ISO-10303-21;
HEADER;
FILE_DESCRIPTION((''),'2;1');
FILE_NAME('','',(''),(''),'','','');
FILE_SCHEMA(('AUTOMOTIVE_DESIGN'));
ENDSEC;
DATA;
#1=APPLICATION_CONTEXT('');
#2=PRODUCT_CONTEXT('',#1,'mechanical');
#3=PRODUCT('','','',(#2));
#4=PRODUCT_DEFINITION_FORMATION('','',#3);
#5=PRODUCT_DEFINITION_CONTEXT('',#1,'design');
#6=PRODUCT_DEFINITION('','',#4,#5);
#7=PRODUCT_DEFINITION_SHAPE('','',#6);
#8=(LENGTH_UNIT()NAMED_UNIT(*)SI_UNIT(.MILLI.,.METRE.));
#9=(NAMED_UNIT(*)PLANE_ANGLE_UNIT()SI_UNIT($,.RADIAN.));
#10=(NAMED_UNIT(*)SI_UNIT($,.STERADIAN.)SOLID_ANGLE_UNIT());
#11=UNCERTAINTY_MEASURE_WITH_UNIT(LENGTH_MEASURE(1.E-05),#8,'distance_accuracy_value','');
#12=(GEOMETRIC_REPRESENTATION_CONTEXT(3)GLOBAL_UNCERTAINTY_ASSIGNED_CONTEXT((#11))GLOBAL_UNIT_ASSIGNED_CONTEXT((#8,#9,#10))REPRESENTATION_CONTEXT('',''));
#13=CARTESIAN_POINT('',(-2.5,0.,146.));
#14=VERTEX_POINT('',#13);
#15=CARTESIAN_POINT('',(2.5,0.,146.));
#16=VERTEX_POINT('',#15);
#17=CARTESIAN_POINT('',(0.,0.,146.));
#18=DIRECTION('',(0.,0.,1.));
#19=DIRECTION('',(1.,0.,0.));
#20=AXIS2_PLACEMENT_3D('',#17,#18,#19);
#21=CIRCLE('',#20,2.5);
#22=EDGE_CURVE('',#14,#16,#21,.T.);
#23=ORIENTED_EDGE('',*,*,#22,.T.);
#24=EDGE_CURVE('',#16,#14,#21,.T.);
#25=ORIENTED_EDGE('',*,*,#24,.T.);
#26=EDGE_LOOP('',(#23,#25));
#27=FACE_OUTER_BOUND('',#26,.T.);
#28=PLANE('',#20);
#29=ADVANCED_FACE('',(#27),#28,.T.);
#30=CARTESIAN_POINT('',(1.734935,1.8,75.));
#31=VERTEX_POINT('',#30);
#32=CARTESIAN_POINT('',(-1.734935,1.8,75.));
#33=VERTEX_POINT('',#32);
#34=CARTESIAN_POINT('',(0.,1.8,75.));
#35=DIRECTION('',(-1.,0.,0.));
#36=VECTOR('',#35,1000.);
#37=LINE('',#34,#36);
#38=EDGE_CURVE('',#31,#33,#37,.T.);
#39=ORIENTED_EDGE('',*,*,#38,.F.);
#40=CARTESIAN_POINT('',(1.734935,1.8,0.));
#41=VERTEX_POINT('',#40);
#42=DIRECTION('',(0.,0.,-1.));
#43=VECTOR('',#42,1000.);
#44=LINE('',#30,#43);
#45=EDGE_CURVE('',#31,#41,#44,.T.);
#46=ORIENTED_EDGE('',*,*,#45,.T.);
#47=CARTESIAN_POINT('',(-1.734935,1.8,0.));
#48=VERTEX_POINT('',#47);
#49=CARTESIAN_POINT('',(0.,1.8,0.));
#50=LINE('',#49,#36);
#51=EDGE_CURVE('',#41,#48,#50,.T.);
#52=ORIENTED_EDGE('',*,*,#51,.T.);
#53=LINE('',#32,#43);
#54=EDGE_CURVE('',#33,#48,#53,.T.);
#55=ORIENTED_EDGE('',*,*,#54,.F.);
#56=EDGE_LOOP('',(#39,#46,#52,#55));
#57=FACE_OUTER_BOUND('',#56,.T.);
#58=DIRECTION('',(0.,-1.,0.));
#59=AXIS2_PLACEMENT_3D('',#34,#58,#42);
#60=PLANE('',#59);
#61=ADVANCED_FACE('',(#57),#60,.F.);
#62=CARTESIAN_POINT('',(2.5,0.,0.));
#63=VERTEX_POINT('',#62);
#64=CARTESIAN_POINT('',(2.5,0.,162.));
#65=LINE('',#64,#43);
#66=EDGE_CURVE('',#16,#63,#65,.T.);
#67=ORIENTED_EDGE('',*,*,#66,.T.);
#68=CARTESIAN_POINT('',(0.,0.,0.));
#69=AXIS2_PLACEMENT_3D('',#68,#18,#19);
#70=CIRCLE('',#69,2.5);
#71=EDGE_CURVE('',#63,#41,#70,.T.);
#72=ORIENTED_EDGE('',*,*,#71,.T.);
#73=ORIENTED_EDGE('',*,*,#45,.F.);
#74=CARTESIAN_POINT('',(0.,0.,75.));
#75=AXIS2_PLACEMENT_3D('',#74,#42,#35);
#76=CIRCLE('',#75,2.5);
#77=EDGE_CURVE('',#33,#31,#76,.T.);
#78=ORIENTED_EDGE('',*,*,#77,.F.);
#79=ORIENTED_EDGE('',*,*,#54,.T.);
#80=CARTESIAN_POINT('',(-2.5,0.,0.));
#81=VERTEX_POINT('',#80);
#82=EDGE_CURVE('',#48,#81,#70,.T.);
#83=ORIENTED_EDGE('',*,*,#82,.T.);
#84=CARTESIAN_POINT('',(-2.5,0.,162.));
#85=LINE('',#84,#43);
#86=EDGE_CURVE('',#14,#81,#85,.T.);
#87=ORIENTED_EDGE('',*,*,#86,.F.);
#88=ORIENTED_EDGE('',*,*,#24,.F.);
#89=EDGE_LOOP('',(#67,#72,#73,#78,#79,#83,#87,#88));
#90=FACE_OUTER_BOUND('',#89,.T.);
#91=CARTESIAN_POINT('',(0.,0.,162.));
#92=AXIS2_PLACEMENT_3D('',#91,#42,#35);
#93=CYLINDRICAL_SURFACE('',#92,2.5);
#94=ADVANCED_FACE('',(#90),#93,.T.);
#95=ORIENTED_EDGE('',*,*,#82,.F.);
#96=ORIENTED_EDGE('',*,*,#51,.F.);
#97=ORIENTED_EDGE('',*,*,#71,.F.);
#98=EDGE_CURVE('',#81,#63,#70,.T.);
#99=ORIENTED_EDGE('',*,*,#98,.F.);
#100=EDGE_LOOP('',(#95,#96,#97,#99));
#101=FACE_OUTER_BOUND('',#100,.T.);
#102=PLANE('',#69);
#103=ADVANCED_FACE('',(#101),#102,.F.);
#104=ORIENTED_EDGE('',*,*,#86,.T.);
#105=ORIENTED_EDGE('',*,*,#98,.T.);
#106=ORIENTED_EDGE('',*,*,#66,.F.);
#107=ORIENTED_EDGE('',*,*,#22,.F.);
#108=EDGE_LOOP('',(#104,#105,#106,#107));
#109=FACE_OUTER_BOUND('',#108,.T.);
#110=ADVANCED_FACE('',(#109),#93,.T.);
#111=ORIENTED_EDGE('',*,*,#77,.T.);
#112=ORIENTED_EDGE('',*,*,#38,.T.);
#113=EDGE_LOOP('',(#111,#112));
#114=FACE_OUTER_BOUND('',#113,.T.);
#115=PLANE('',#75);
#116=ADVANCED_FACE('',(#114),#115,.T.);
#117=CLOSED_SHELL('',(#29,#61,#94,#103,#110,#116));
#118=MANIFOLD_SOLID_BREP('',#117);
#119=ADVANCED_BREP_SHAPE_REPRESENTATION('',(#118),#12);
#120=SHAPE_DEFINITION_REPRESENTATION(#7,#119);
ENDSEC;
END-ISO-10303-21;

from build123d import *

# Parameters (mm, degrees)
SKETCH1_R           = 2.5
BOSS_EXTRUDE1_DEPTH = 162
CUT_EXTRUDE1_DEPTH  = 75
CUT_EXTRUDE2_START  = -16
SKETCH3_R           = 2.5
CUT_EXTRUDE2_DEPTH  = 16


with BuildPart() as part:
    # Sketch1 → Boss-Extrude1 (new body)
    with BuildSketch(Plane.XY):
        Circle(SKETCH1_R)
    extrude(amount=BOSS_EXTRUDE1_DEPTH)

    # Sketch2 → Cut-Extrude1 (cut)
    with BuildSketch(Plane(origin=(0, 0, 0), x_dir=(-1, 0, 0), z_dir=(0, 0, -1))):
        with BuildLine():
            Line((0, 1.8), (1.734935157, 1.8))
            ThreePointArc((1.734935157, 1.8), (0, 2.5), (-1.734935157, 1.8))
            Line((-1.734935157, 1.8), (0, 1.8))
        make_face()
    extrude(amount=-CUT_EXTRUDE1_DEPTH, mode=Mode.SUBTRACT)

    # Sketch3 → Cut-Extrude2 (cut)
    with BuildSketch(Plane.XY.offset(162).offset(CUT_EXTRUDE2_START)):
        with Locations(Location((0, 0, 0), (0, 0, 133.945519562))):
            Circle(SKETCH3_R)
    extrude(amount=CUT_EXTRUDE2_DEPTH, mode=Mode.SUBTRACT)


solid = part.part
